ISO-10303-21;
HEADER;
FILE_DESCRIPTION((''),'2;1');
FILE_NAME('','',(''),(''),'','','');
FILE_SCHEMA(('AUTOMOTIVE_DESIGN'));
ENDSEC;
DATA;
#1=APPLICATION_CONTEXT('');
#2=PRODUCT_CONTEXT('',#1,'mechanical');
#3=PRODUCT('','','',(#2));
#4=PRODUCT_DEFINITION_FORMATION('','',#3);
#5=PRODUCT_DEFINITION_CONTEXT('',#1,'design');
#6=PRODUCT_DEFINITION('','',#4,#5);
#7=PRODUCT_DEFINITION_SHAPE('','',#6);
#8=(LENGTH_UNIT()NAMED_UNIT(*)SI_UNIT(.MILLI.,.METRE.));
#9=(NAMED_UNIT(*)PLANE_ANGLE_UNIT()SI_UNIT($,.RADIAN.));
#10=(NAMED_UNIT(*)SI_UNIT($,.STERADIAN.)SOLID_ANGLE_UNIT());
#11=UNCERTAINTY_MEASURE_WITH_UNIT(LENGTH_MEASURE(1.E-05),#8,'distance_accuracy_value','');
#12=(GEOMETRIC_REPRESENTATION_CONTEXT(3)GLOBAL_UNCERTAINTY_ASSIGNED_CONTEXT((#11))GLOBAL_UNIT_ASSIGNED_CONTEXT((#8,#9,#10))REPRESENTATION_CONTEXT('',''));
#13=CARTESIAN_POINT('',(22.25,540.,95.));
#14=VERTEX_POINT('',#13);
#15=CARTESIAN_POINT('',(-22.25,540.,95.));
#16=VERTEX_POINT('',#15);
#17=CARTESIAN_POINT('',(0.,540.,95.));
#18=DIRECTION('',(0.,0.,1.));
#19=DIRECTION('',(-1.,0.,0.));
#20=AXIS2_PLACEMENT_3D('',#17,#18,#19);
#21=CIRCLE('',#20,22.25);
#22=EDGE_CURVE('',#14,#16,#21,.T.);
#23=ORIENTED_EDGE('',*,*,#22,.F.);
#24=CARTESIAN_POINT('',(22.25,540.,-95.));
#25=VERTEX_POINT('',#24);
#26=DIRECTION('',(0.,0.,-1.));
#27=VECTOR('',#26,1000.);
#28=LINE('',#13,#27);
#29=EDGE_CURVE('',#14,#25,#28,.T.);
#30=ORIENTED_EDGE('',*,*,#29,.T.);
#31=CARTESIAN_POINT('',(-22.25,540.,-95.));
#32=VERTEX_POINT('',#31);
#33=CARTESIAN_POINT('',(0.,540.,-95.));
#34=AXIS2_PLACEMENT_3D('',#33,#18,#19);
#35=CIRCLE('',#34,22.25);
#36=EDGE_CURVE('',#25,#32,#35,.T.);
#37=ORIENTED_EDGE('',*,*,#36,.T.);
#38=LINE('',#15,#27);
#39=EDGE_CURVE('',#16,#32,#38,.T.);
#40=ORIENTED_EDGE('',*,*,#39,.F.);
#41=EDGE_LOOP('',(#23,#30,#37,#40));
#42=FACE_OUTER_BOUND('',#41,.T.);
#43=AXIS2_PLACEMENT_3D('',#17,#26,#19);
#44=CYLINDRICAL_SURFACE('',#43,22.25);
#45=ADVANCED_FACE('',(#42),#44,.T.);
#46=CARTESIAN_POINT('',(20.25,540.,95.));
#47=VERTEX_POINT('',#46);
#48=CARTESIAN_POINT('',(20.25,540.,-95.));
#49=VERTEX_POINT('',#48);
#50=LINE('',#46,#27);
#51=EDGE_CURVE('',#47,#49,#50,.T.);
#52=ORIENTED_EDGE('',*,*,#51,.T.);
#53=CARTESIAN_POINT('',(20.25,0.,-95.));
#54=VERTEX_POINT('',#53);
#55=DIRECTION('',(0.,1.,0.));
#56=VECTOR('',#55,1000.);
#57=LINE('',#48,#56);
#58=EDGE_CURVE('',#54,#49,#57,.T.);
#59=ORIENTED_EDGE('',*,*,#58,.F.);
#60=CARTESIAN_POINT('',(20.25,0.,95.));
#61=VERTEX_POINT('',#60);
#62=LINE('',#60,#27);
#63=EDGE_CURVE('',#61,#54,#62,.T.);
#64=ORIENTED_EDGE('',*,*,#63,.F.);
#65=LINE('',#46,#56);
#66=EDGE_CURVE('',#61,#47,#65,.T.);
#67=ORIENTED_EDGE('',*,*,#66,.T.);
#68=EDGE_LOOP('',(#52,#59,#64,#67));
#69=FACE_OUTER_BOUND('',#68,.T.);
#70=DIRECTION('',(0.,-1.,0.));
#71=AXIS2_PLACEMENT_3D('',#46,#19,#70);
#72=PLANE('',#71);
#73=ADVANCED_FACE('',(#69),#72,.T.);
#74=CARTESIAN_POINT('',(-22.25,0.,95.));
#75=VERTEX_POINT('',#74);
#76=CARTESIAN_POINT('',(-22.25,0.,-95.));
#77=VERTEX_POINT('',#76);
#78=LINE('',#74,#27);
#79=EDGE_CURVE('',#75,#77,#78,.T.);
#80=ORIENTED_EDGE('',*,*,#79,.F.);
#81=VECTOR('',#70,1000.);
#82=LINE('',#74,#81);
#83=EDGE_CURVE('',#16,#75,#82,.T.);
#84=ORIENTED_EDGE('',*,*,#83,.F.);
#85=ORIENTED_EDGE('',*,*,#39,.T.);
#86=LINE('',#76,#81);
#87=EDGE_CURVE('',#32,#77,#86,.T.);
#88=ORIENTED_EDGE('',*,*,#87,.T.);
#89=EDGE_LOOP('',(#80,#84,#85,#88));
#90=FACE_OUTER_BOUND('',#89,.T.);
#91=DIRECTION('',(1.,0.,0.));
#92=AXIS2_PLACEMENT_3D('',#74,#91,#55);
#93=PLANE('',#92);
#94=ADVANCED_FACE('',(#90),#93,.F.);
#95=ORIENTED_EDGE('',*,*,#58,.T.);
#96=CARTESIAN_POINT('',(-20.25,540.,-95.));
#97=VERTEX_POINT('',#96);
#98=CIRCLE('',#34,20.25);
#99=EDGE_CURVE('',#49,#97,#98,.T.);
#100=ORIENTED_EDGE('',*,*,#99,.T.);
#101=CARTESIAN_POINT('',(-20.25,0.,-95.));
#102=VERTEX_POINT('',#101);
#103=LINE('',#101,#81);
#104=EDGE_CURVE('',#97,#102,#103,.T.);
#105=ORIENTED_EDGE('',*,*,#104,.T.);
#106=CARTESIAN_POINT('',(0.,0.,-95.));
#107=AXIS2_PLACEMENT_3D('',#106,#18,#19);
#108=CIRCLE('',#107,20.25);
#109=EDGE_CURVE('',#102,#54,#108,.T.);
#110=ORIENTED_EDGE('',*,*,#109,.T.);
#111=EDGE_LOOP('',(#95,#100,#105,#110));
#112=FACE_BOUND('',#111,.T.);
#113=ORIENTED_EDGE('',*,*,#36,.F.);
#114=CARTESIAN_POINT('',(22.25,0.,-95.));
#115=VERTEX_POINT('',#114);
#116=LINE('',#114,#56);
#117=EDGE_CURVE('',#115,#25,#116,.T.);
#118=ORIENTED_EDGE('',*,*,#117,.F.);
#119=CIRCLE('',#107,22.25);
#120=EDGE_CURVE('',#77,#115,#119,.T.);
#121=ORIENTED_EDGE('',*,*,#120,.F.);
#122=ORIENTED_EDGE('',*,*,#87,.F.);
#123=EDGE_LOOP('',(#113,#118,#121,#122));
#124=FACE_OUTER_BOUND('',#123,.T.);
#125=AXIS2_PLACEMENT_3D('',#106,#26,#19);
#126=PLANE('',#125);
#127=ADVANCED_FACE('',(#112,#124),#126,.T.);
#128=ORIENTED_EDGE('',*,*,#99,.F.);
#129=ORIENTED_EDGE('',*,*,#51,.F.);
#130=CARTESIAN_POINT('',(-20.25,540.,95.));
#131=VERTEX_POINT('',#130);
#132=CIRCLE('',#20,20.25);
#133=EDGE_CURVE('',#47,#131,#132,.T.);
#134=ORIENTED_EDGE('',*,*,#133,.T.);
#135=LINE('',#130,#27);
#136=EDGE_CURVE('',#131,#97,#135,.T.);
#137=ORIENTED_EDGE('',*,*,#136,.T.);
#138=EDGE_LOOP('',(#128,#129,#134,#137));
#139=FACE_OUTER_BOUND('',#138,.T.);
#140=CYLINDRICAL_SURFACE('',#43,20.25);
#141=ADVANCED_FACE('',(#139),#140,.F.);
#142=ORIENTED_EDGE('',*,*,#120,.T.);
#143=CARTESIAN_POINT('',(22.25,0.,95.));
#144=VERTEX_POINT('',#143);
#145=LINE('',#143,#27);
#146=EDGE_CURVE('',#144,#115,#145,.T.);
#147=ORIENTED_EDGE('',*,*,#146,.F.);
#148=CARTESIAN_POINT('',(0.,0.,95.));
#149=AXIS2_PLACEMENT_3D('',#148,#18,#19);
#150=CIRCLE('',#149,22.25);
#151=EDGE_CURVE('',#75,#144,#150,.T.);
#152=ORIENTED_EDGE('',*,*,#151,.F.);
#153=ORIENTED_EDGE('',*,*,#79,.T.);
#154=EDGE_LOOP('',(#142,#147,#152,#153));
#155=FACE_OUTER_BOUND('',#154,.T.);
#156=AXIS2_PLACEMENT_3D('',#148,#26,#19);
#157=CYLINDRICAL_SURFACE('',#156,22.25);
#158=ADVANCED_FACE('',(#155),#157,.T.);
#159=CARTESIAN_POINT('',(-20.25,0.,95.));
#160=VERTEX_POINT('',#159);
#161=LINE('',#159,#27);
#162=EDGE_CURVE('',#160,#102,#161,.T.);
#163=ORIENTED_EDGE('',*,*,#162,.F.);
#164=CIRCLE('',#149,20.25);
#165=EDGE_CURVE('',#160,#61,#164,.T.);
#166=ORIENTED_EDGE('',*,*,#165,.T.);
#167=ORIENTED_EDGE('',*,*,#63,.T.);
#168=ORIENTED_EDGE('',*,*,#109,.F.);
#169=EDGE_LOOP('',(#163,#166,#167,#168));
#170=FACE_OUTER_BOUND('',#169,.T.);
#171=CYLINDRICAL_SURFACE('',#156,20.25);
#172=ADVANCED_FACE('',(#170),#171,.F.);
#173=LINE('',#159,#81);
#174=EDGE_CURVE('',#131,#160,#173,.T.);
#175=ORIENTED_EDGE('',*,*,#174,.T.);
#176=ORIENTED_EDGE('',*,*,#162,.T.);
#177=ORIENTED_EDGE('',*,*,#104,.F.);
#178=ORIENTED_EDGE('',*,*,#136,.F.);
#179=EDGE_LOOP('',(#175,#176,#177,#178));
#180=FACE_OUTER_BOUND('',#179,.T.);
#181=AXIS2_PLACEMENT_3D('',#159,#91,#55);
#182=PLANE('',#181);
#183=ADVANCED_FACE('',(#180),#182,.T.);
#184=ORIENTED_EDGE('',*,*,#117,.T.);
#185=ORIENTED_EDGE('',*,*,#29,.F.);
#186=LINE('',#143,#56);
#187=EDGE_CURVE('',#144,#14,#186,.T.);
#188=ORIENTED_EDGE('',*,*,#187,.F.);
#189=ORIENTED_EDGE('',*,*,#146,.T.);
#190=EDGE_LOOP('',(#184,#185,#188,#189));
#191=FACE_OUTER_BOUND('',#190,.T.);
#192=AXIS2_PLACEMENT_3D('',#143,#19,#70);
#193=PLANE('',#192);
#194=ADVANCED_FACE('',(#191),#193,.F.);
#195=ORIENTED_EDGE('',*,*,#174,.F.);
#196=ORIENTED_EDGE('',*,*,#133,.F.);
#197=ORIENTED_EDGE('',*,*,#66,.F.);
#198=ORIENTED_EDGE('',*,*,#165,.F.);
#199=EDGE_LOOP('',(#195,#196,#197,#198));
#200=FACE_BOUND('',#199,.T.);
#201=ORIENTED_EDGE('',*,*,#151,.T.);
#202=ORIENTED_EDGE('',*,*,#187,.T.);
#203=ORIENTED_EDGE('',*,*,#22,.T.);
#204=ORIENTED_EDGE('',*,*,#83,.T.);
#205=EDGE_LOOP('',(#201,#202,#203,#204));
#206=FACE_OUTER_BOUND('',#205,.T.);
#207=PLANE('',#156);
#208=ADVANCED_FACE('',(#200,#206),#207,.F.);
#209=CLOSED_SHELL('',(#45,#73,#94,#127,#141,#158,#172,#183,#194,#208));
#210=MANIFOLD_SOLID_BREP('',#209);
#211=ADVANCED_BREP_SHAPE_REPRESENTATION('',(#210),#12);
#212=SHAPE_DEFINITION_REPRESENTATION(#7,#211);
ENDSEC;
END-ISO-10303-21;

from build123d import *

# Parameters (mm, degrees)
EXTRUDE_1_DEPTH = 95


with BuildPart() as part:
    # 草图2 → 拉伸-薄壁1 (new, symmetric)
    with BuildSketch(Plane.XY):
        with BuildLine():
            Line((22.25, 540), (22.25, 0))
            ThreePointArc((22.25, 0), (0, -22.25), (-22.25, 0))
            Line((-22.25, 0), (-22.25, 540))
            ThreePointArc((-22.25, 540), (0, 562.25), (22.25, 540))
        make_face()
        with BuildLine():
            Line((20.25, 540), (20.25, 0))
            ThreePointArc((20.25, 0), (0, -20.25), (-20.25, 0))
            Line((-20.25, 0), (-20.25, 540))
            ThreePointArc((-20.25, 540), (0, 560.25), (20.25, 540))
        make_face(mode=Mode.SUBTRACT)
    extrude(amount=EXTRUDE_1_DEPTH, both=True)


solid = part.part
